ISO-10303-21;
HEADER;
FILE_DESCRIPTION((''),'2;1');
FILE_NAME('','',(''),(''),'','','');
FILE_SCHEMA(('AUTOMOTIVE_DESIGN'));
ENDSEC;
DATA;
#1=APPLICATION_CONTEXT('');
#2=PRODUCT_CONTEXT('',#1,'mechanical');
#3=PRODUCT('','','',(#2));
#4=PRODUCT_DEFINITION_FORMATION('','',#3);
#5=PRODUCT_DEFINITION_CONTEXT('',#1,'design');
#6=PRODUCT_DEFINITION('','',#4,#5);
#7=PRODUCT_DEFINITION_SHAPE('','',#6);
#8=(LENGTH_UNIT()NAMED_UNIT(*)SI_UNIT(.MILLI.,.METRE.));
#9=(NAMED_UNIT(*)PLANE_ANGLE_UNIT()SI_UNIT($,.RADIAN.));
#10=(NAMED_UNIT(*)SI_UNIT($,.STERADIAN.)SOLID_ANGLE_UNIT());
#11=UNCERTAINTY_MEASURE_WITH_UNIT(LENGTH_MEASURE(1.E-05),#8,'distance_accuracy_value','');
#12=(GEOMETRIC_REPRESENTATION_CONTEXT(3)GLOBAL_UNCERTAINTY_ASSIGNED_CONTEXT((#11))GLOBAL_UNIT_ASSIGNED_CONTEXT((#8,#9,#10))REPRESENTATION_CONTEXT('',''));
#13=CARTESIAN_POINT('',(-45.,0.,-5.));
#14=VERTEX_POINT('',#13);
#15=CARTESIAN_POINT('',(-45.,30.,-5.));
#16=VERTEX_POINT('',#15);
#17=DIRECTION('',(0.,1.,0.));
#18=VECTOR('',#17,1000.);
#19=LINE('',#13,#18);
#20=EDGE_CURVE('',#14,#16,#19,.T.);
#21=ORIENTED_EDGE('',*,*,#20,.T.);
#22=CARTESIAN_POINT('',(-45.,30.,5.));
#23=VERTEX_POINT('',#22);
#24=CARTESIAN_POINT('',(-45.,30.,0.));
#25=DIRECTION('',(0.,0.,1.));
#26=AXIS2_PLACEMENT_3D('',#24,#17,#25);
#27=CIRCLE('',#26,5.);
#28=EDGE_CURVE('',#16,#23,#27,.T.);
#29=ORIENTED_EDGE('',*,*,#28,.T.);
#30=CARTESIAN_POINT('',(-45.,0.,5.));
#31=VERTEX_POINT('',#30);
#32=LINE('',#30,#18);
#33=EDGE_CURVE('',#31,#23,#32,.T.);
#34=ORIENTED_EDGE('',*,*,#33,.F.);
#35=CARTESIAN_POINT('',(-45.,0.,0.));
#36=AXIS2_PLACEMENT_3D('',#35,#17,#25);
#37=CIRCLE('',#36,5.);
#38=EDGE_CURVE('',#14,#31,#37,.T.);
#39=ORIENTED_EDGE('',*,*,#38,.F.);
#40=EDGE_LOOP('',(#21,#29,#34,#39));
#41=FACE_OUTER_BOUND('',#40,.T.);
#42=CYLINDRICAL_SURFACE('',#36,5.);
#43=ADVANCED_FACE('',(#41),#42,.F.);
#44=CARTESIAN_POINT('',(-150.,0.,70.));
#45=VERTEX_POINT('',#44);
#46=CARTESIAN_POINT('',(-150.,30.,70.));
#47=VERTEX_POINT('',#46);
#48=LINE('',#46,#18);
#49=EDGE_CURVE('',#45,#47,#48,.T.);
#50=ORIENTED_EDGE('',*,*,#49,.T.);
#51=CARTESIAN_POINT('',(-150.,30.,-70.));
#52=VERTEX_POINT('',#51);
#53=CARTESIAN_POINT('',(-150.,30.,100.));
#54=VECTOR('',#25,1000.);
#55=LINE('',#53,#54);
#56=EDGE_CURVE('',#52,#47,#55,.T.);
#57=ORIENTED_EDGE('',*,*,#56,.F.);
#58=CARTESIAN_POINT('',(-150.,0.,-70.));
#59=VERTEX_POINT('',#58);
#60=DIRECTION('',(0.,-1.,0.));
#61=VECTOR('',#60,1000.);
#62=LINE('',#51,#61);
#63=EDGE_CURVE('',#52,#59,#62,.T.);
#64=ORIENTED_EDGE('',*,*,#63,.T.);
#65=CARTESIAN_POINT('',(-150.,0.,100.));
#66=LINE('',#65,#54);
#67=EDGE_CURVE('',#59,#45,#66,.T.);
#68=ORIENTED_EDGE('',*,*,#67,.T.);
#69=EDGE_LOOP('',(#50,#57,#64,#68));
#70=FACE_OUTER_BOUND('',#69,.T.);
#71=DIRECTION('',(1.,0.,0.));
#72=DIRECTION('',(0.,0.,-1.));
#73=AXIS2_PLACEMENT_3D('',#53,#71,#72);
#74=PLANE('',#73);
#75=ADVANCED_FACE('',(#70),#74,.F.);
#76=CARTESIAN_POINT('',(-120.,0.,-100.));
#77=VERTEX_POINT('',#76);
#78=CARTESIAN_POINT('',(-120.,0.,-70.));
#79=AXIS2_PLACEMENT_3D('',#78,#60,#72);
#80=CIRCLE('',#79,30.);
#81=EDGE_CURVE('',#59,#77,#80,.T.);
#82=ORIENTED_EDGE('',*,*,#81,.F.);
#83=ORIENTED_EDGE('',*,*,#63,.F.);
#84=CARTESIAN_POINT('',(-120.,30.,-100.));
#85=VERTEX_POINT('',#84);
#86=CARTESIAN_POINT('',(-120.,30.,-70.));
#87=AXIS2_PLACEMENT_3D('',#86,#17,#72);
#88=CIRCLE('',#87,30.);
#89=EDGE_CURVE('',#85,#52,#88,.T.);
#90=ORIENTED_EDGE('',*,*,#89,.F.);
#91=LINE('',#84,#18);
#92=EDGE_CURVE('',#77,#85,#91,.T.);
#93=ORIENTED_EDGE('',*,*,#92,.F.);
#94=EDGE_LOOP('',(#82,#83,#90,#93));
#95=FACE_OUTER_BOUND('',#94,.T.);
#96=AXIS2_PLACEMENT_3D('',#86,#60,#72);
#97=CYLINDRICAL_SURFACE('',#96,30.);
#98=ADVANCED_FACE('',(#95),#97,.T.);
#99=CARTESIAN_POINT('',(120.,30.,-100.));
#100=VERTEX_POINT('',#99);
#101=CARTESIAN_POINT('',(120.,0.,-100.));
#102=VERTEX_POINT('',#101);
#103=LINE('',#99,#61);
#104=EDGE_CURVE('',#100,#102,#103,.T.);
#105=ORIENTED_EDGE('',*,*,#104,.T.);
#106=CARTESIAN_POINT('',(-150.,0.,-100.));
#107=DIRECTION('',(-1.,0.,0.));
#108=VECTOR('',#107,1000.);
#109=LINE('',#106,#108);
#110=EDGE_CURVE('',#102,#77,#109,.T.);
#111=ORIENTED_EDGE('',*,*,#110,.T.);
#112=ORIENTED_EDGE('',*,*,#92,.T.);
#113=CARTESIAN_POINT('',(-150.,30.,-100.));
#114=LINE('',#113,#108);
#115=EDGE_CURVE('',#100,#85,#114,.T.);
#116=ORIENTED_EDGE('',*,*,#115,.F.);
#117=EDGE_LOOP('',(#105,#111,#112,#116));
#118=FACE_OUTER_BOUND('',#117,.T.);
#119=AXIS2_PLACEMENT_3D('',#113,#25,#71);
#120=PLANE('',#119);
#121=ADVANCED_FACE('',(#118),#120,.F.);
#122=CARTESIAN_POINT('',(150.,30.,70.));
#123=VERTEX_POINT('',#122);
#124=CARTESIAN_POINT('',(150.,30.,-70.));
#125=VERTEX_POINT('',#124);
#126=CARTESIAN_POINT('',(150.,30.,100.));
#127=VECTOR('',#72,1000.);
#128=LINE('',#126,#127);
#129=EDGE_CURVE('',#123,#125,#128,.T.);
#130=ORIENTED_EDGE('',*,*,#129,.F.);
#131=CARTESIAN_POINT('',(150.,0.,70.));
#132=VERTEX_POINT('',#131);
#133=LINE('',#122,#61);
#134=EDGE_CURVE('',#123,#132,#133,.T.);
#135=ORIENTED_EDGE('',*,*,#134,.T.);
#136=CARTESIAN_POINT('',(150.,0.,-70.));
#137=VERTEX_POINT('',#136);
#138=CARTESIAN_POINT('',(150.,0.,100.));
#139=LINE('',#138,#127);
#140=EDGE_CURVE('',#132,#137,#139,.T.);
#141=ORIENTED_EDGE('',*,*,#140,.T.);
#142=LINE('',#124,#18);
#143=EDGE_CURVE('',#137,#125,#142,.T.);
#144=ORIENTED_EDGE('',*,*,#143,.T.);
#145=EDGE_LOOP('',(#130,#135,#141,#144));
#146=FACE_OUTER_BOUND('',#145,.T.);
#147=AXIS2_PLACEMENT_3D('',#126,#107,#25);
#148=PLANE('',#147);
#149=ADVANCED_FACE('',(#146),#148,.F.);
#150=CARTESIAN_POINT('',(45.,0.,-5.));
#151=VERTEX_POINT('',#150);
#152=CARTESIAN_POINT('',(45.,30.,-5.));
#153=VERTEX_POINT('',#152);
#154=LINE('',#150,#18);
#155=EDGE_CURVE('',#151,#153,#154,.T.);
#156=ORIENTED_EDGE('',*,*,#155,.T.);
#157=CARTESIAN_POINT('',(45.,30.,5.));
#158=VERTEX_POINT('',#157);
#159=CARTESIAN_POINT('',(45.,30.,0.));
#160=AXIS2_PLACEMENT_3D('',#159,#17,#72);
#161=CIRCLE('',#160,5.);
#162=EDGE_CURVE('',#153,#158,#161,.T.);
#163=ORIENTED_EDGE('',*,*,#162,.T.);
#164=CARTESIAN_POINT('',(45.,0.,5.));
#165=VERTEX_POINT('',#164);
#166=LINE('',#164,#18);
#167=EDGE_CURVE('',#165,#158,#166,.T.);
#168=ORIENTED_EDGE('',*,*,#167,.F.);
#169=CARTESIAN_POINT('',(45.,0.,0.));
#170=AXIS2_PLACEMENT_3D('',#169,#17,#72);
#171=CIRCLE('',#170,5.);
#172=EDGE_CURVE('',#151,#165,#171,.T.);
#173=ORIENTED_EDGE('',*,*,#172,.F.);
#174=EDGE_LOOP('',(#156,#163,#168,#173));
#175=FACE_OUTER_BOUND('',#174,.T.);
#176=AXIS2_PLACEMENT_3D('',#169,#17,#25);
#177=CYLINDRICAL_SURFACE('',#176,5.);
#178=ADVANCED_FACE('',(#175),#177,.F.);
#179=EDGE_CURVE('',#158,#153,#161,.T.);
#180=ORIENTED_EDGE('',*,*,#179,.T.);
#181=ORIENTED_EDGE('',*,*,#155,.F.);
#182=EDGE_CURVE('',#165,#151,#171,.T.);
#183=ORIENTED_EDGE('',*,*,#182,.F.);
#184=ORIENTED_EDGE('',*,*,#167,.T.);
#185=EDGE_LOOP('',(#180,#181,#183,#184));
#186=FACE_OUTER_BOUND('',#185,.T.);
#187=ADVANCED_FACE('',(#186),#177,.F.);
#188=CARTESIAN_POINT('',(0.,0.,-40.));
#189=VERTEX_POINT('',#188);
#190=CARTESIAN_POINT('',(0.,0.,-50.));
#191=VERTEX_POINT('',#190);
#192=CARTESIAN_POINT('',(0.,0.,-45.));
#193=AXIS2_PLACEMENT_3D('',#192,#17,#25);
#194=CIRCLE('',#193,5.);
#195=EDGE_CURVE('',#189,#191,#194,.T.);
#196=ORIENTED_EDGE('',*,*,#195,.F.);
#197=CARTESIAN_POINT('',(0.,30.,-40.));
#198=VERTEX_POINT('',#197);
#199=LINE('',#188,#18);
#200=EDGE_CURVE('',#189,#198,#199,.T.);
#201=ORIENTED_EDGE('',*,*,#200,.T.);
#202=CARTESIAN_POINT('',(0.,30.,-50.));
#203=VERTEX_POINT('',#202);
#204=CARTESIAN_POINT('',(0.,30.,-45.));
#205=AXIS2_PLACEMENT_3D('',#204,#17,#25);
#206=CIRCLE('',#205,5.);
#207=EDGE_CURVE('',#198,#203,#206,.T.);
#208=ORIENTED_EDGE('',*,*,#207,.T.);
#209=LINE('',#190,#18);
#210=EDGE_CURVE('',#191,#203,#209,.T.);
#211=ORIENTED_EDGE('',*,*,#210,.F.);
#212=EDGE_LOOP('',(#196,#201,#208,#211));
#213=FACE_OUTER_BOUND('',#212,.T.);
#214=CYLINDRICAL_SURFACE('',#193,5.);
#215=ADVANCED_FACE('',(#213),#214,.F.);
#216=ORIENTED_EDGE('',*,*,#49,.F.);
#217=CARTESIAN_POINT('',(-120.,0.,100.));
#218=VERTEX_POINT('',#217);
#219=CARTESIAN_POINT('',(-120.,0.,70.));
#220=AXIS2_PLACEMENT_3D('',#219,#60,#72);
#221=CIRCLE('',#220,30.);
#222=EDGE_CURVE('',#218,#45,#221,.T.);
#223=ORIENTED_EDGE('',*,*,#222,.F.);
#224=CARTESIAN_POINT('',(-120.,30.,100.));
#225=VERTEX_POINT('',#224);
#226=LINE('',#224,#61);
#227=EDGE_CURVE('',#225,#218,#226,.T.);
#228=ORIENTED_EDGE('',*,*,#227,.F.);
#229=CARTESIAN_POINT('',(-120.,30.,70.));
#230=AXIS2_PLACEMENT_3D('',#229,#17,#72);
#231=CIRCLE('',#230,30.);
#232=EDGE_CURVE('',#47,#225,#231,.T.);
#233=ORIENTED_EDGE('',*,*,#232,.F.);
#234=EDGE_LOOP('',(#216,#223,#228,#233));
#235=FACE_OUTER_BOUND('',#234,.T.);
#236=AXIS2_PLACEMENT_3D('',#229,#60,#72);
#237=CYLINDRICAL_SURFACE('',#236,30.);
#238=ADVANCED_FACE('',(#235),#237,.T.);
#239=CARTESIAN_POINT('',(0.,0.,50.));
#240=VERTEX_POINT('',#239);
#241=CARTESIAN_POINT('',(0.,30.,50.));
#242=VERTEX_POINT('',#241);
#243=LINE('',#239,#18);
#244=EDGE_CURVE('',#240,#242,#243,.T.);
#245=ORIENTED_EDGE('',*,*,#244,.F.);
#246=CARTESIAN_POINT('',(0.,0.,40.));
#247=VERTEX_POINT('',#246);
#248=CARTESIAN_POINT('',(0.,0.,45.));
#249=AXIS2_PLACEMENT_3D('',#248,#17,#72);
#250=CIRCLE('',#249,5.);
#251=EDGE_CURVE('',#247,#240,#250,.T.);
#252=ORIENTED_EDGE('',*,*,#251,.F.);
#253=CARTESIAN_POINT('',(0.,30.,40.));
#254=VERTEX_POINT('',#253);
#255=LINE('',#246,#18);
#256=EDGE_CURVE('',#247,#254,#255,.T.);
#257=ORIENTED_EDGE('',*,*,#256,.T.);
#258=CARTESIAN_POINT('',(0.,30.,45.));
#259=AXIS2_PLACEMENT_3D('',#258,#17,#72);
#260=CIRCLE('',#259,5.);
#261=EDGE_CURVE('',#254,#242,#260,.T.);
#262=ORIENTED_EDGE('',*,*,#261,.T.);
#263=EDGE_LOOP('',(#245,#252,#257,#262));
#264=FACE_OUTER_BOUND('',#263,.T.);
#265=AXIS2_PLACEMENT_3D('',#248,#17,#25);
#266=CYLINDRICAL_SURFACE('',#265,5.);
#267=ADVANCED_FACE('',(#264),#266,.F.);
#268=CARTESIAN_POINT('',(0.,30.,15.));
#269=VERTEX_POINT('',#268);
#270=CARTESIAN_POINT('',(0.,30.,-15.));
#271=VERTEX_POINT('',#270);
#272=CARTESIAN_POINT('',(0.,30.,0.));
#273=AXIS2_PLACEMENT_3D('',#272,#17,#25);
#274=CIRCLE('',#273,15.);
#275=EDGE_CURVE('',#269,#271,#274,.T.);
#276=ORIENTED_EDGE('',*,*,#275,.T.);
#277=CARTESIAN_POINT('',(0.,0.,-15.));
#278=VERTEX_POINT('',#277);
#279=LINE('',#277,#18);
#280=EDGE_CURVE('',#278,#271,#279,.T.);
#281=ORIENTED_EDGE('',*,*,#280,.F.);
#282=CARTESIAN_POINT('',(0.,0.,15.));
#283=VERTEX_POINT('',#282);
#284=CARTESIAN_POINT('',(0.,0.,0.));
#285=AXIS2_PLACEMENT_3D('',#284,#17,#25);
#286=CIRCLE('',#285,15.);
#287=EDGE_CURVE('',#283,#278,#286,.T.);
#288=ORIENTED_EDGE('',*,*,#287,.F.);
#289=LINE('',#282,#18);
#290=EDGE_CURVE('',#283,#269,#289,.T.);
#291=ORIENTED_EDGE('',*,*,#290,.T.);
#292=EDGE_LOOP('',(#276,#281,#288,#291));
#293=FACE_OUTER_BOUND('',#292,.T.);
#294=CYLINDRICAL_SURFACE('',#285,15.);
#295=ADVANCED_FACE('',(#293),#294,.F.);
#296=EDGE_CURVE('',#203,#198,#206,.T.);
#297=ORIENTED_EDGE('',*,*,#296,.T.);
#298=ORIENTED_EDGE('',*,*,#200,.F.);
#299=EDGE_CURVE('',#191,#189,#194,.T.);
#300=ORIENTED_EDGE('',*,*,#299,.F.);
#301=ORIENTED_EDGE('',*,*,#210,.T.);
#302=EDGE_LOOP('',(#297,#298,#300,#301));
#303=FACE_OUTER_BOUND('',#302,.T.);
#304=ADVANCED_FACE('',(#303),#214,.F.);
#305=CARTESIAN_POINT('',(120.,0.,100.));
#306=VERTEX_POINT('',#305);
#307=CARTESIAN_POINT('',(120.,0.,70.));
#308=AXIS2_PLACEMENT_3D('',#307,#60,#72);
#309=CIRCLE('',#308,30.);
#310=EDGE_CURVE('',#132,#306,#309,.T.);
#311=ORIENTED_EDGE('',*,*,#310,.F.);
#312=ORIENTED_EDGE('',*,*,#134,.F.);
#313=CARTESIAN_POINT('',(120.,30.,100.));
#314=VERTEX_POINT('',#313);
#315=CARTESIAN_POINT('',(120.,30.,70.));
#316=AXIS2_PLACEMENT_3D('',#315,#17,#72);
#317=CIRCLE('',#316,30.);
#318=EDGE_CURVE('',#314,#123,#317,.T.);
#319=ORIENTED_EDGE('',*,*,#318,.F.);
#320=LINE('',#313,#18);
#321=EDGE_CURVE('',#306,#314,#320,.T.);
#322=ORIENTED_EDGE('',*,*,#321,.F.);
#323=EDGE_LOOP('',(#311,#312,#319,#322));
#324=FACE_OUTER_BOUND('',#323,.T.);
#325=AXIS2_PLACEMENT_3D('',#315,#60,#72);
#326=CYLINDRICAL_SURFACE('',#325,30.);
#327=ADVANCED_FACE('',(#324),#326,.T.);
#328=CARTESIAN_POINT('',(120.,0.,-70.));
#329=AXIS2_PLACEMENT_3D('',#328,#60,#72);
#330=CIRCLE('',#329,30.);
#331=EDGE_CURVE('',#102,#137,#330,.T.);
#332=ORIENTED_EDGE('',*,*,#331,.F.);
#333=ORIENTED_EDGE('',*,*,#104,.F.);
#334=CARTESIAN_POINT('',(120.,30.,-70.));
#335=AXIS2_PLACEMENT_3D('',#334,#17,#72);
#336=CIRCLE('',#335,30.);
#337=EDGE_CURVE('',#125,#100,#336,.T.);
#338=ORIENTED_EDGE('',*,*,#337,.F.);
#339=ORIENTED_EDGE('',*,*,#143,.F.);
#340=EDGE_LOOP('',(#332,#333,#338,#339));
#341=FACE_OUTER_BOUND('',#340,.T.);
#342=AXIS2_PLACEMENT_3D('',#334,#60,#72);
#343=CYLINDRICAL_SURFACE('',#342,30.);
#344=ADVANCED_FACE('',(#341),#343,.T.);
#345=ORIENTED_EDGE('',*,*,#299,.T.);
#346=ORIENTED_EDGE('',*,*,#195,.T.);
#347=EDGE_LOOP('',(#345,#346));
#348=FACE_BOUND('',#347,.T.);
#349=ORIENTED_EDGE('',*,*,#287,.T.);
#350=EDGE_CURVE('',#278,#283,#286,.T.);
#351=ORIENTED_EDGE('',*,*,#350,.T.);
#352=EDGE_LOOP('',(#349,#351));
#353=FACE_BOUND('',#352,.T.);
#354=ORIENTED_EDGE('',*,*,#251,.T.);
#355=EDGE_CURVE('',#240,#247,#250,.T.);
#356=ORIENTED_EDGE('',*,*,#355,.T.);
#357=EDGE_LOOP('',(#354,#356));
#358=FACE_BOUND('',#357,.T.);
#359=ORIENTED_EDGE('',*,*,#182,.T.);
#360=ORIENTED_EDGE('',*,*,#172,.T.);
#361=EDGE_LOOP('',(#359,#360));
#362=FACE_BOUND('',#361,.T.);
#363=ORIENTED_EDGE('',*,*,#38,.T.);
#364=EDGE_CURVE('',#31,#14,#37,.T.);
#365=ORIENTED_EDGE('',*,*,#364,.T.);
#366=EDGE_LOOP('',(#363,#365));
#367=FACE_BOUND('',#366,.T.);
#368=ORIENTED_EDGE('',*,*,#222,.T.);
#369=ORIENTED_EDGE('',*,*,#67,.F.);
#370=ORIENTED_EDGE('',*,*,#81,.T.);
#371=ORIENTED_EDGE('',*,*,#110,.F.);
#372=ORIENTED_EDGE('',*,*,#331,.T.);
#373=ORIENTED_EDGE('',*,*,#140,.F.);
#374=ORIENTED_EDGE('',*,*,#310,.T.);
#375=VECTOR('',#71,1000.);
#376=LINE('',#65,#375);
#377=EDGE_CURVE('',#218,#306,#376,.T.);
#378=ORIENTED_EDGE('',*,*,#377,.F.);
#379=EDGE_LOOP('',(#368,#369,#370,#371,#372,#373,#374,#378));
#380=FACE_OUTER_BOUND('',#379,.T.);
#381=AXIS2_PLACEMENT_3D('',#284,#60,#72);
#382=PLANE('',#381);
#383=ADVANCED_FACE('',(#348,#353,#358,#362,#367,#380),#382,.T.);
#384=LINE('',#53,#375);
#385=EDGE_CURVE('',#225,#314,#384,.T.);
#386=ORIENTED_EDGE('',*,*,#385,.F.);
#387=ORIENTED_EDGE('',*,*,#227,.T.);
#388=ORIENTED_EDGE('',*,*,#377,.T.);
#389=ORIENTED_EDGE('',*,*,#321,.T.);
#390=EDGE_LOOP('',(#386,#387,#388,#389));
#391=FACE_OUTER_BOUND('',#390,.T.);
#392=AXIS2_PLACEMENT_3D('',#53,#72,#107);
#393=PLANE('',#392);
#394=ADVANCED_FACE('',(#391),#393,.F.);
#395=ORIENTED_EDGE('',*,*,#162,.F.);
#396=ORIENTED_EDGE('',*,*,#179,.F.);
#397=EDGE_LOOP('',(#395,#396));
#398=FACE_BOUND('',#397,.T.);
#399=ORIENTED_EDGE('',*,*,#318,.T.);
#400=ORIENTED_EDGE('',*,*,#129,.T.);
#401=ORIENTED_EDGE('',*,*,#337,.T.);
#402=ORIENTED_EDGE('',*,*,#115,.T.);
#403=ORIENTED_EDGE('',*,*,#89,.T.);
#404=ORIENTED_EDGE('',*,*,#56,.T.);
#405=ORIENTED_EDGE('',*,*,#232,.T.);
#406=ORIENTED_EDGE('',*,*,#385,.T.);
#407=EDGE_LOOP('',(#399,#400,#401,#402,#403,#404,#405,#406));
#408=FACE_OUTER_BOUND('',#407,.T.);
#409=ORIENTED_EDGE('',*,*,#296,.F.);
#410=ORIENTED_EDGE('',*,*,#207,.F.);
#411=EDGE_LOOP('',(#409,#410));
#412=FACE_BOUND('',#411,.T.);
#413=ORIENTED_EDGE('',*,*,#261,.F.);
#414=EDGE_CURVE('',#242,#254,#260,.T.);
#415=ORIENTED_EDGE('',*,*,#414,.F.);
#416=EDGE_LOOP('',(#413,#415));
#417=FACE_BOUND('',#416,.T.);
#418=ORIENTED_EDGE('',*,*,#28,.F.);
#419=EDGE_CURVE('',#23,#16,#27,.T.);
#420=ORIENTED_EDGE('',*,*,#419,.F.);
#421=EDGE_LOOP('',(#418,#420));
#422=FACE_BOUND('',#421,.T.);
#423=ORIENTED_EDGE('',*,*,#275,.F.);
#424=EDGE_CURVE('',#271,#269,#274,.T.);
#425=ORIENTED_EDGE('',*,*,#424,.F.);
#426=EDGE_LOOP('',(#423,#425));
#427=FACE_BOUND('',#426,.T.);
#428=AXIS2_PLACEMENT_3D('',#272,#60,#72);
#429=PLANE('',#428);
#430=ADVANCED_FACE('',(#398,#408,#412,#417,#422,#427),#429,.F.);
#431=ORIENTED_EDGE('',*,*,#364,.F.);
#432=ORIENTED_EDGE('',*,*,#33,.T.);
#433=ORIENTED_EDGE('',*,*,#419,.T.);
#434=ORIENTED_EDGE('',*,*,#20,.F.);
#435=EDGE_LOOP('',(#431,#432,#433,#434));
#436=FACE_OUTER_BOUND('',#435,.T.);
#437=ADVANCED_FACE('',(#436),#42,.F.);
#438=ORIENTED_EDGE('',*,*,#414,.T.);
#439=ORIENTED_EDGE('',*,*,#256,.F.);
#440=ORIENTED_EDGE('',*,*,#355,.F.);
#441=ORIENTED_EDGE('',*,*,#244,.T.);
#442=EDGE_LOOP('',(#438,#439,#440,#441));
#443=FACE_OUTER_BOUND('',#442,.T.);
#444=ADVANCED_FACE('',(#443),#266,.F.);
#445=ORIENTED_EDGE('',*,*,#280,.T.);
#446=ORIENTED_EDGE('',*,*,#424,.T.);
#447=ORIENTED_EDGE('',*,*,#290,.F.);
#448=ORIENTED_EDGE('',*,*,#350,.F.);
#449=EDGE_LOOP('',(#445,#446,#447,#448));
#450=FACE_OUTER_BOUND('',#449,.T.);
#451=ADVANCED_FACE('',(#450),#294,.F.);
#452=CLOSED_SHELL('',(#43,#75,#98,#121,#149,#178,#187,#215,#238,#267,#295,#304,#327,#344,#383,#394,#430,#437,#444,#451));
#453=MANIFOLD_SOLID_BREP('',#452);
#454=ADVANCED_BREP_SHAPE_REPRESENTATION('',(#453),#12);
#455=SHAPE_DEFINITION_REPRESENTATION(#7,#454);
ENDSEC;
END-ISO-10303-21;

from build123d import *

# Parameters (mm, degrees)
SKETCH1_W           = 300
SKETCH1_H           = 200
BOSS_EXTRUDE1_DEPTH = 30
SKETCH2_R           = 15
SKETCH2_R_2         = 5
CUT_EXTRUDE1_DEPTH  = 30
FILLET1_R           = 30


with BuildPart() as part:
    # Sketch1 → Boss-Extrude1 (new body)
    with BuildSketch(Plane(origin=(0, 0, 0), x_dir=(1, 0, 0), z_dir=(0, 1, 0))):
        Rectangle(SKETCH1_W, SKETCH1_H)
    extrude(amount=BOSS_EXTRUDE1_DEPTH)

    # Sketch2 → Cut-Extrude1 (cut)
    with BuildSketch(Plane(origin=(0, 30, 0), x_dir=(1, 0, 0), z_dir=(0, 1, 0))):
        with Locations(Location((0, 0, 0), (0, 0, 270))):
            Circle(SKETCH2_R)
        with Locations(Location((0, 45, 0), (0, 0, 270))):
            Circle(SKETCH2_R_2)
        with Locations(Location((-45, 0, 0), (0, 0, 270))):
            Circle(SKETCH2_R_2)
        with Locations(Location((0, -45, 0), (0, 0, 90))):
            Circle(SKETCH2_R_2)
        with Locations(Location((45, 0, 0), (0, 0, 90))):
            Circle(SKETCH2_R_2)
    extrude(amount=-CUT_EXTRUDE1_DEPTH, mode=Mode.SUBTRACT)

    # Fillet1
    fillet1_edges = [part.edges().sort_by_distance(p)[0] for p in [
        (150, 15, 100),
        (-150, 15, 100),
        (-150, 15, -100),
        (150, 15, -100),
    ]]
    fillet(fillet1_edges, radius=FILLET1_R)


solid = part.part
